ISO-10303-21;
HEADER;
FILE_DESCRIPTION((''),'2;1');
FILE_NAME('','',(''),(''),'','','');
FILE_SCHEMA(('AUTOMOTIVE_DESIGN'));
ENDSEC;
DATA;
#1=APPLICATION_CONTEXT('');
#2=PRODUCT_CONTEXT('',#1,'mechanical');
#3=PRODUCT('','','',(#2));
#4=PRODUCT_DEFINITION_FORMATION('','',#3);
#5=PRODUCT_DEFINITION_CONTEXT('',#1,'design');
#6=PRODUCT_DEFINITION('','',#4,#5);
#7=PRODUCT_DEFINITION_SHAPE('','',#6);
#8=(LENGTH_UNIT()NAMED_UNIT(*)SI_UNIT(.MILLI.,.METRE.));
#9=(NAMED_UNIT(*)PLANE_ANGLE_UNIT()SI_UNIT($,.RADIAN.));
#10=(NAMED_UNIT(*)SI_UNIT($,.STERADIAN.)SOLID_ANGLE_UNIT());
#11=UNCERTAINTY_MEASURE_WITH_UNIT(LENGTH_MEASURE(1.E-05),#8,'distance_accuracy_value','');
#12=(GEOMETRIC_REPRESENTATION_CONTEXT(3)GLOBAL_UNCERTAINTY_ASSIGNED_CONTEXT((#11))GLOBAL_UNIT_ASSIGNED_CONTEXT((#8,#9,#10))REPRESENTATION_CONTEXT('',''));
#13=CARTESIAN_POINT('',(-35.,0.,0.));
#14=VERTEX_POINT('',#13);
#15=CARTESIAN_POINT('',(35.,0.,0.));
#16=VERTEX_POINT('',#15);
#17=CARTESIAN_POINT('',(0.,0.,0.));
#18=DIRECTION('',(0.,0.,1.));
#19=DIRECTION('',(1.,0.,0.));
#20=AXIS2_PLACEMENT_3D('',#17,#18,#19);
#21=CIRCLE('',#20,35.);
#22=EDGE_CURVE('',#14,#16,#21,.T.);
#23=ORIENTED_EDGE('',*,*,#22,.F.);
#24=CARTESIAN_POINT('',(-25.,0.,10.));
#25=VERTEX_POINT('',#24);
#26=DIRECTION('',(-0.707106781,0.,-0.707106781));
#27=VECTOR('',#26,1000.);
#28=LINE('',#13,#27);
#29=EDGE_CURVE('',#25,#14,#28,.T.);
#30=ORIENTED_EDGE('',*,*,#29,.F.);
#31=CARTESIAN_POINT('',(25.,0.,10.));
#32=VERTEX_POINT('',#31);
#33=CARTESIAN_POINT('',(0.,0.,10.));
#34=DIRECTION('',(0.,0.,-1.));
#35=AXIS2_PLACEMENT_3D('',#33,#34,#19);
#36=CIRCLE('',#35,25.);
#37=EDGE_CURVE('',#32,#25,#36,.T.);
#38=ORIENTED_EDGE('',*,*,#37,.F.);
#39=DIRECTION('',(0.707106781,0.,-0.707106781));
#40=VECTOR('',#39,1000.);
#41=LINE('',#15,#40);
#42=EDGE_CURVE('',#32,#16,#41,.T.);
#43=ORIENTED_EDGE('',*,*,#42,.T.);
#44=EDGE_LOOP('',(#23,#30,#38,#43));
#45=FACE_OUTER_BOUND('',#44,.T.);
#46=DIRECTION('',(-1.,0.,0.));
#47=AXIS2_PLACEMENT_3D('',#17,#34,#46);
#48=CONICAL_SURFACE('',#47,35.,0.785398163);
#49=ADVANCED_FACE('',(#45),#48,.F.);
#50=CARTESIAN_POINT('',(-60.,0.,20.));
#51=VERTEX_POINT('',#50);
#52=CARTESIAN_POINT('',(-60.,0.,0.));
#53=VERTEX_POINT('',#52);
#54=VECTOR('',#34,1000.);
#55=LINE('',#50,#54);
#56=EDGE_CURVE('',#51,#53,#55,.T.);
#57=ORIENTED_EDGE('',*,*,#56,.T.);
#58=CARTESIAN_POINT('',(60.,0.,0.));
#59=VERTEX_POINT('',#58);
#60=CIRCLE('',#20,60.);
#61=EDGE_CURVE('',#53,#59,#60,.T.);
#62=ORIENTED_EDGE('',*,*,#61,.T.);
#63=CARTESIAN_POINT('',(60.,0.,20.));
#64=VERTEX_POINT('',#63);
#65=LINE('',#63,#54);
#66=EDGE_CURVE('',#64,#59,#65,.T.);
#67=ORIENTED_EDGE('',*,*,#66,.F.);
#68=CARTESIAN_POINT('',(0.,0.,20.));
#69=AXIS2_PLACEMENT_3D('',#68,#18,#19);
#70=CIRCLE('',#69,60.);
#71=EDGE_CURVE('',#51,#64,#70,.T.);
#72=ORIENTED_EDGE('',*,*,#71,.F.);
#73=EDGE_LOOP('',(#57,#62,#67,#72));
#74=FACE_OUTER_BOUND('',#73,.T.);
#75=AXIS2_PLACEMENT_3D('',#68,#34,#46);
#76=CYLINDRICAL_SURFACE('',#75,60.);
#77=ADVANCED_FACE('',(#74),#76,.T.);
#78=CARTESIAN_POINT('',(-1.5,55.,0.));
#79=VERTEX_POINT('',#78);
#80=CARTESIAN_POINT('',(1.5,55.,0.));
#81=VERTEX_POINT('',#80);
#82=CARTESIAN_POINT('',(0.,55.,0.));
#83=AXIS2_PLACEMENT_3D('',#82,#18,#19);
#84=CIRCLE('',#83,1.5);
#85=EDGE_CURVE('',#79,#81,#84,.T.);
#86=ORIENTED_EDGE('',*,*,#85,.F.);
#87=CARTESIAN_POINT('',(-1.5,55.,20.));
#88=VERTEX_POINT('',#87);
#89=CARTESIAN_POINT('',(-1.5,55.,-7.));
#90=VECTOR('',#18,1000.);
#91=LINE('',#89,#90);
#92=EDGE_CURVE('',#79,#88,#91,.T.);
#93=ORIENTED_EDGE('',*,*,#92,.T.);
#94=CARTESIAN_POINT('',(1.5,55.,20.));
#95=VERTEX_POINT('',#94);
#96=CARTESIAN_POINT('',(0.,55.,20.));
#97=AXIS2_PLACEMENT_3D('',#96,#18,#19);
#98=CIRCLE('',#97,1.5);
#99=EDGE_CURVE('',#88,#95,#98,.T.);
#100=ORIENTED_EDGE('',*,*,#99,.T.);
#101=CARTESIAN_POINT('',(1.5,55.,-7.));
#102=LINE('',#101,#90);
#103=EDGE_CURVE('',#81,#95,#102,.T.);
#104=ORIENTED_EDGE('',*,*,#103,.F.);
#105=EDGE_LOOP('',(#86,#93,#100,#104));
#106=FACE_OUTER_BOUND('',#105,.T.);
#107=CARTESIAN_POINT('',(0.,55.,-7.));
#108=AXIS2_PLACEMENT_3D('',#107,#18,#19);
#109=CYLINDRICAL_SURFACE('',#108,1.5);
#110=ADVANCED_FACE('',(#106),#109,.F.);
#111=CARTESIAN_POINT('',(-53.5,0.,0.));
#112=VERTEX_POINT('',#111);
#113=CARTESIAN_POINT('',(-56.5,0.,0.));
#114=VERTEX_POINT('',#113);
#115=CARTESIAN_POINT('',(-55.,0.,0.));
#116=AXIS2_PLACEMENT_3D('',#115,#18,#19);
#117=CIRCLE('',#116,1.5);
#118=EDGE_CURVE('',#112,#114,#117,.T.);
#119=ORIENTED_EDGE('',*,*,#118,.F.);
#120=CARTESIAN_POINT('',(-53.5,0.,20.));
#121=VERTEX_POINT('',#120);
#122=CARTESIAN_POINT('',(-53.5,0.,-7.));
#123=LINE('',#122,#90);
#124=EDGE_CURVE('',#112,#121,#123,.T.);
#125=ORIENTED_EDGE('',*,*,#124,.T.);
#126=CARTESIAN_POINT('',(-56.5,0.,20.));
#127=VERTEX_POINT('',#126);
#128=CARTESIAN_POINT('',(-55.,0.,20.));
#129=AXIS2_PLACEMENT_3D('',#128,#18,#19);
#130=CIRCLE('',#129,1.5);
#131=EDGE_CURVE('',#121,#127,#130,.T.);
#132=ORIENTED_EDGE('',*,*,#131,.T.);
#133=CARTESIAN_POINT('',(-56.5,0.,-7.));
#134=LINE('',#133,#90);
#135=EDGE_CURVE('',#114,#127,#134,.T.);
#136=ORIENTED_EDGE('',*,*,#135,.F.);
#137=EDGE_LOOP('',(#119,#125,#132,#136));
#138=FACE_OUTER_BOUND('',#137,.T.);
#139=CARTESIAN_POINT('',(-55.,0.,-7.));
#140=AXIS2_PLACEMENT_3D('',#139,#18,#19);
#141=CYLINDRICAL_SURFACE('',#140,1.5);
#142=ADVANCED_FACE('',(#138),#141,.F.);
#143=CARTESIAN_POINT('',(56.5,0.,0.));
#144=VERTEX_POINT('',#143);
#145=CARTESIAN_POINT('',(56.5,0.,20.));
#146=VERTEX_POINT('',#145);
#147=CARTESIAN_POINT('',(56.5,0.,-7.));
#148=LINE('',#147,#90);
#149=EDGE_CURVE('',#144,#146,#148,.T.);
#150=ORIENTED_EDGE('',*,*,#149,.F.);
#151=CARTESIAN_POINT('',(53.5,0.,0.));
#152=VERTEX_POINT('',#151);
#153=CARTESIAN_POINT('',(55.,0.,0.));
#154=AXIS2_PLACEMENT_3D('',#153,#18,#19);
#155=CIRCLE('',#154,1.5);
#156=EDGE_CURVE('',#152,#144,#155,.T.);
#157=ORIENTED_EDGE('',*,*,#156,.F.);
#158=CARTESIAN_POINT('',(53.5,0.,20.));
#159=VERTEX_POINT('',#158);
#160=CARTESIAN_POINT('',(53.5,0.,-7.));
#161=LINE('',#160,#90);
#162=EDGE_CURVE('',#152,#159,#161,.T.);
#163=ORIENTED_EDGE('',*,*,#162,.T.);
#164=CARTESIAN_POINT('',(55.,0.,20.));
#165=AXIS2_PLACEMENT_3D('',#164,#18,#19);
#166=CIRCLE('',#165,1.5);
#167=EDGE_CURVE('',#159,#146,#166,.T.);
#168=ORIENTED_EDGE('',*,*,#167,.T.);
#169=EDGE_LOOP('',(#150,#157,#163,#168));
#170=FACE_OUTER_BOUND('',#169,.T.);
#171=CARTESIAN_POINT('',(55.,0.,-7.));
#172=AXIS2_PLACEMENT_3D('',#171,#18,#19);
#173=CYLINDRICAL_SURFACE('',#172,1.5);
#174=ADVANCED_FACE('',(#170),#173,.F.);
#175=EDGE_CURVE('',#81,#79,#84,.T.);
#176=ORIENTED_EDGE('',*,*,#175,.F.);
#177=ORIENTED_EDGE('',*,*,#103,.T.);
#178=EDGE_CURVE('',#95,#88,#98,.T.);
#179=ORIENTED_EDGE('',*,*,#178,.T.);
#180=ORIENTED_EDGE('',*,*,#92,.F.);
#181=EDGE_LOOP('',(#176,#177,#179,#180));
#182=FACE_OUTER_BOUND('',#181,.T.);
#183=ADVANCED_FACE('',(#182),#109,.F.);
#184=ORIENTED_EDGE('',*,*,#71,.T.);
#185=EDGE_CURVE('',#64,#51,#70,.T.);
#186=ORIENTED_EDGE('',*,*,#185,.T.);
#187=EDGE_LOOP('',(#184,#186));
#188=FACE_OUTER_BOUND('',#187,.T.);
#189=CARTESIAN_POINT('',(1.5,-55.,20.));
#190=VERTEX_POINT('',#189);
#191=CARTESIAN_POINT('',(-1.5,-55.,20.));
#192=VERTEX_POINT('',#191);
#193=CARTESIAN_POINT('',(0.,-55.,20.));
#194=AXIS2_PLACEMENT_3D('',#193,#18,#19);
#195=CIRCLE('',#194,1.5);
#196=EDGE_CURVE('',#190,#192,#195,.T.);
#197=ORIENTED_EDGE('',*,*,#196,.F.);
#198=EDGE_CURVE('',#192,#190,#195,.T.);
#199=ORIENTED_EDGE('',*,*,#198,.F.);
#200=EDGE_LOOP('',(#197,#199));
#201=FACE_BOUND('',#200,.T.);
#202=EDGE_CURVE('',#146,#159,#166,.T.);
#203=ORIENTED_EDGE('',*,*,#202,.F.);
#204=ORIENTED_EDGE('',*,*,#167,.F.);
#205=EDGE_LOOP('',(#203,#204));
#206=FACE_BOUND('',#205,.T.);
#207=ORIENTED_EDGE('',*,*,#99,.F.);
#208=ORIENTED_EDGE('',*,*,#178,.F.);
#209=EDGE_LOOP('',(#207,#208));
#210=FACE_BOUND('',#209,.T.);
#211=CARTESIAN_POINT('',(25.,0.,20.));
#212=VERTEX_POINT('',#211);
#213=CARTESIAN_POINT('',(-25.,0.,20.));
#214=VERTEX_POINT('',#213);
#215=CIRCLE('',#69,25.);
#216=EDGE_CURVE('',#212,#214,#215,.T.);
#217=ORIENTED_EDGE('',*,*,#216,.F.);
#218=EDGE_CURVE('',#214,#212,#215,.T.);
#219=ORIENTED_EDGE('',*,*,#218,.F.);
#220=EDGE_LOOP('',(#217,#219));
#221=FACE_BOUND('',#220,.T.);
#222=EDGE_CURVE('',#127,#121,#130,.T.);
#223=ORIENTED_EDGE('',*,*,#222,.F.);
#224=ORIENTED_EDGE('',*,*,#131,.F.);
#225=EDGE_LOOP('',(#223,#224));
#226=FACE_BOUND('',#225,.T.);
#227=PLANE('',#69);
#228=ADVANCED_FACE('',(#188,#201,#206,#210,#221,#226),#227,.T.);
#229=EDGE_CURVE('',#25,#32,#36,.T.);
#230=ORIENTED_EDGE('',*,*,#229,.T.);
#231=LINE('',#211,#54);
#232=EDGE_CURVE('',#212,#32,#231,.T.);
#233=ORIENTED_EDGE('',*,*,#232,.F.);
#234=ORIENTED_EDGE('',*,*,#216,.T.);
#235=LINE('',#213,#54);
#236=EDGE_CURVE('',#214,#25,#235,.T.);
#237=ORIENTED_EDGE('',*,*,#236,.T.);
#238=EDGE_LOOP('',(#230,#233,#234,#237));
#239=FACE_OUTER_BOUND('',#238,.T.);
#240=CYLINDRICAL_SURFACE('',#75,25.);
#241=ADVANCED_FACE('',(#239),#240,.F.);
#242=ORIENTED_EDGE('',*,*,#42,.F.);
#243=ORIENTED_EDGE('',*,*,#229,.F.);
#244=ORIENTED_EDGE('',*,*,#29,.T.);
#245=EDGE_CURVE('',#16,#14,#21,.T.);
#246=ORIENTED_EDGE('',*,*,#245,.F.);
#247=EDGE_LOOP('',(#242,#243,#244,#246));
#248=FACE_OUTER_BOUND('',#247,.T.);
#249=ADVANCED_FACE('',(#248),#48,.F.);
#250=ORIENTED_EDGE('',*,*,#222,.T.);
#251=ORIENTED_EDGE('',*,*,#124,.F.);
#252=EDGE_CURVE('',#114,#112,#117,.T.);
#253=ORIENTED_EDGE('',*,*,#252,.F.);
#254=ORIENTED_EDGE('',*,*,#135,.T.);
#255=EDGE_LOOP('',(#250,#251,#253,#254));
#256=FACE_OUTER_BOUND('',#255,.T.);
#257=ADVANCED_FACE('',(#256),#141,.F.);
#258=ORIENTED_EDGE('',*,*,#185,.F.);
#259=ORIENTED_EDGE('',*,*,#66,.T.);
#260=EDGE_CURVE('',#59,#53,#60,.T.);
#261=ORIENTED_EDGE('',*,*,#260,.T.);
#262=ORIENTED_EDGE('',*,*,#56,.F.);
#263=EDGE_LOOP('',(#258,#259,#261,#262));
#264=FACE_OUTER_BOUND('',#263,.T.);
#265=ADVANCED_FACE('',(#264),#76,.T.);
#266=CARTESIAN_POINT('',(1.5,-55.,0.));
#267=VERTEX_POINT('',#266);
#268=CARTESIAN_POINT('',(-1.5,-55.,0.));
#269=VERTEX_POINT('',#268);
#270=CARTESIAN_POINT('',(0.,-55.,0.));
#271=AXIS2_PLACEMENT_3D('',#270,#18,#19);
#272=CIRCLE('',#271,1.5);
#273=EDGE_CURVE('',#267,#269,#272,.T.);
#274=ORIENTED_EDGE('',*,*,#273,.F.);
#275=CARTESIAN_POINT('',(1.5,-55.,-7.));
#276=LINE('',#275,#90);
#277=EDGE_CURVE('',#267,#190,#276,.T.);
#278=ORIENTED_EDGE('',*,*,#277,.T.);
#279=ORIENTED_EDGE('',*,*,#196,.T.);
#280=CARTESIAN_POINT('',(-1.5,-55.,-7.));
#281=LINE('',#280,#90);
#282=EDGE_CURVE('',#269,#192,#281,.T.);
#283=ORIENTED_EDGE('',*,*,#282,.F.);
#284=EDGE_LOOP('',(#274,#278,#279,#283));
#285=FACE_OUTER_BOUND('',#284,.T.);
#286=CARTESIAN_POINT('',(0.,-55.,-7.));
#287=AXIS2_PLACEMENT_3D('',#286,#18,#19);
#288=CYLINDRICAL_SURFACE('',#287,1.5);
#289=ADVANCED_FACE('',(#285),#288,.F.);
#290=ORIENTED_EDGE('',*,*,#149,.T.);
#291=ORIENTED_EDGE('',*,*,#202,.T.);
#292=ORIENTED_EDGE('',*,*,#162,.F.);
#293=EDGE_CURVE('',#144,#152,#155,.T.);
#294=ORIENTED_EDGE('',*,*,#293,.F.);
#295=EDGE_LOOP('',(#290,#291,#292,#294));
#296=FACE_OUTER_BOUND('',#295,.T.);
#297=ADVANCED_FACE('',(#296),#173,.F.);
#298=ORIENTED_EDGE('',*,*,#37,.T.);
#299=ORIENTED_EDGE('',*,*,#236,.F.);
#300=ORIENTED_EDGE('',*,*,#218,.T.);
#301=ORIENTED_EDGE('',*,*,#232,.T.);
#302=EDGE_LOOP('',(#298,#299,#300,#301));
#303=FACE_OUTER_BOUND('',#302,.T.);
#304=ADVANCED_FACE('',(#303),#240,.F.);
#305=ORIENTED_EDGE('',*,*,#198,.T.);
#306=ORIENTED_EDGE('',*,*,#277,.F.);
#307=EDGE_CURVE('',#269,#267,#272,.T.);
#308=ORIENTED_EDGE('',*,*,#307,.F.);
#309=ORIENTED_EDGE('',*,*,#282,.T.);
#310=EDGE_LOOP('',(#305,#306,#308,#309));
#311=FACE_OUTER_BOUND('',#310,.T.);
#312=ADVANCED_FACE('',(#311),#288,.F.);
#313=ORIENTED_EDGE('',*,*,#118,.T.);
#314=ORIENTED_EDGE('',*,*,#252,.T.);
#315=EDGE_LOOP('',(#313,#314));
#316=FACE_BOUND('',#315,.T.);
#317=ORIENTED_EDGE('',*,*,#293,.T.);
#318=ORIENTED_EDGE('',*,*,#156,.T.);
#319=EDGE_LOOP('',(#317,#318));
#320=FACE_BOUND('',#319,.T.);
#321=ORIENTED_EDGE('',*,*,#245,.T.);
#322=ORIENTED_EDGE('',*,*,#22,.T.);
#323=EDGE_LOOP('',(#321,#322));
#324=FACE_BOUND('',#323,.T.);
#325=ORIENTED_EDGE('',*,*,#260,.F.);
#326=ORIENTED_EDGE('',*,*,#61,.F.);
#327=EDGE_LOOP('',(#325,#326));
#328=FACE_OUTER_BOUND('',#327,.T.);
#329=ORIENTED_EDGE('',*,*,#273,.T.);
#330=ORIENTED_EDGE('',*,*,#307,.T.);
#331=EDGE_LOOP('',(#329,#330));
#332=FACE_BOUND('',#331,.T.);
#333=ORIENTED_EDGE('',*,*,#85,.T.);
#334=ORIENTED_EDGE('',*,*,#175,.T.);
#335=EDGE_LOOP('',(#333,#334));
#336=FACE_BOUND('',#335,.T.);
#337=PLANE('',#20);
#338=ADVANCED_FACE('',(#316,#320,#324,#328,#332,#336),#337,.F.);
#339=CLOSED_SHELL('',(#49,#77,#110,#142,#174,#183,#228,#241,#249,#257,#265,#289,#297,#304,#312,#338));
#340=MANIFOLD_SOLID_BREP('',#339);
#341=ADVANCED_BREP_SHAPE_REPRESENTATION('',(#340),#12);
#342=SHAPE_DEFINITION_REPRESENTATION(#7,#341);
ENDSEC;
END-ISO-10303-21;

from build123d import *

# Parameters (mm, degrees)
SKETCH_1_R          = 60
SKETCH_1_R_2        = 25
EXTRUDE_1_DEPTH     = 20
CHAMFER_1_SIZE      = 10
SKETCH_2_R          = 1.5
CUT_EXTRUDE_1_DEPTH = 27


with BuildPart() as part:
    # 草图1 → 凸台-拉伸1 (new body)
    with BuildSketch(Plane.XY):
        Circle(SKETCH_1_R)
        Circle(SKETCH_1_R_2, mode=Mode.SUBTRACT)
    extrude(amount=EXTRUDE_1_DEPTH)

    # 倒角1
    chamfer_1_edges = [part.edges().sort_by_distance(p)[0] for p in [
        (-25, 0, 0),
    ]]
    chamfer(chamfer_1_edges, length=CHAMFER_1_SIZE)

    # 草图2 → 切除-拉伸1 (cut)
    with BuildSketch(Plane.XY.offset(20)):
        with Locations((0, 55)):
            Circle(SKETCH_2_R)
        with Locations((55, 0)):
            Circle(SKETCH_2_R)
        with Locations((0, -55)):
            Circle(SKETCH_2_R)
        with Locations((-55, 0)):
            Circle(SKETCH_2_R)
    extrude(amount=-CUT_EXTRUDE_1_DEPTH, mode=Mode.SUBTRACT)


solid = part.part
